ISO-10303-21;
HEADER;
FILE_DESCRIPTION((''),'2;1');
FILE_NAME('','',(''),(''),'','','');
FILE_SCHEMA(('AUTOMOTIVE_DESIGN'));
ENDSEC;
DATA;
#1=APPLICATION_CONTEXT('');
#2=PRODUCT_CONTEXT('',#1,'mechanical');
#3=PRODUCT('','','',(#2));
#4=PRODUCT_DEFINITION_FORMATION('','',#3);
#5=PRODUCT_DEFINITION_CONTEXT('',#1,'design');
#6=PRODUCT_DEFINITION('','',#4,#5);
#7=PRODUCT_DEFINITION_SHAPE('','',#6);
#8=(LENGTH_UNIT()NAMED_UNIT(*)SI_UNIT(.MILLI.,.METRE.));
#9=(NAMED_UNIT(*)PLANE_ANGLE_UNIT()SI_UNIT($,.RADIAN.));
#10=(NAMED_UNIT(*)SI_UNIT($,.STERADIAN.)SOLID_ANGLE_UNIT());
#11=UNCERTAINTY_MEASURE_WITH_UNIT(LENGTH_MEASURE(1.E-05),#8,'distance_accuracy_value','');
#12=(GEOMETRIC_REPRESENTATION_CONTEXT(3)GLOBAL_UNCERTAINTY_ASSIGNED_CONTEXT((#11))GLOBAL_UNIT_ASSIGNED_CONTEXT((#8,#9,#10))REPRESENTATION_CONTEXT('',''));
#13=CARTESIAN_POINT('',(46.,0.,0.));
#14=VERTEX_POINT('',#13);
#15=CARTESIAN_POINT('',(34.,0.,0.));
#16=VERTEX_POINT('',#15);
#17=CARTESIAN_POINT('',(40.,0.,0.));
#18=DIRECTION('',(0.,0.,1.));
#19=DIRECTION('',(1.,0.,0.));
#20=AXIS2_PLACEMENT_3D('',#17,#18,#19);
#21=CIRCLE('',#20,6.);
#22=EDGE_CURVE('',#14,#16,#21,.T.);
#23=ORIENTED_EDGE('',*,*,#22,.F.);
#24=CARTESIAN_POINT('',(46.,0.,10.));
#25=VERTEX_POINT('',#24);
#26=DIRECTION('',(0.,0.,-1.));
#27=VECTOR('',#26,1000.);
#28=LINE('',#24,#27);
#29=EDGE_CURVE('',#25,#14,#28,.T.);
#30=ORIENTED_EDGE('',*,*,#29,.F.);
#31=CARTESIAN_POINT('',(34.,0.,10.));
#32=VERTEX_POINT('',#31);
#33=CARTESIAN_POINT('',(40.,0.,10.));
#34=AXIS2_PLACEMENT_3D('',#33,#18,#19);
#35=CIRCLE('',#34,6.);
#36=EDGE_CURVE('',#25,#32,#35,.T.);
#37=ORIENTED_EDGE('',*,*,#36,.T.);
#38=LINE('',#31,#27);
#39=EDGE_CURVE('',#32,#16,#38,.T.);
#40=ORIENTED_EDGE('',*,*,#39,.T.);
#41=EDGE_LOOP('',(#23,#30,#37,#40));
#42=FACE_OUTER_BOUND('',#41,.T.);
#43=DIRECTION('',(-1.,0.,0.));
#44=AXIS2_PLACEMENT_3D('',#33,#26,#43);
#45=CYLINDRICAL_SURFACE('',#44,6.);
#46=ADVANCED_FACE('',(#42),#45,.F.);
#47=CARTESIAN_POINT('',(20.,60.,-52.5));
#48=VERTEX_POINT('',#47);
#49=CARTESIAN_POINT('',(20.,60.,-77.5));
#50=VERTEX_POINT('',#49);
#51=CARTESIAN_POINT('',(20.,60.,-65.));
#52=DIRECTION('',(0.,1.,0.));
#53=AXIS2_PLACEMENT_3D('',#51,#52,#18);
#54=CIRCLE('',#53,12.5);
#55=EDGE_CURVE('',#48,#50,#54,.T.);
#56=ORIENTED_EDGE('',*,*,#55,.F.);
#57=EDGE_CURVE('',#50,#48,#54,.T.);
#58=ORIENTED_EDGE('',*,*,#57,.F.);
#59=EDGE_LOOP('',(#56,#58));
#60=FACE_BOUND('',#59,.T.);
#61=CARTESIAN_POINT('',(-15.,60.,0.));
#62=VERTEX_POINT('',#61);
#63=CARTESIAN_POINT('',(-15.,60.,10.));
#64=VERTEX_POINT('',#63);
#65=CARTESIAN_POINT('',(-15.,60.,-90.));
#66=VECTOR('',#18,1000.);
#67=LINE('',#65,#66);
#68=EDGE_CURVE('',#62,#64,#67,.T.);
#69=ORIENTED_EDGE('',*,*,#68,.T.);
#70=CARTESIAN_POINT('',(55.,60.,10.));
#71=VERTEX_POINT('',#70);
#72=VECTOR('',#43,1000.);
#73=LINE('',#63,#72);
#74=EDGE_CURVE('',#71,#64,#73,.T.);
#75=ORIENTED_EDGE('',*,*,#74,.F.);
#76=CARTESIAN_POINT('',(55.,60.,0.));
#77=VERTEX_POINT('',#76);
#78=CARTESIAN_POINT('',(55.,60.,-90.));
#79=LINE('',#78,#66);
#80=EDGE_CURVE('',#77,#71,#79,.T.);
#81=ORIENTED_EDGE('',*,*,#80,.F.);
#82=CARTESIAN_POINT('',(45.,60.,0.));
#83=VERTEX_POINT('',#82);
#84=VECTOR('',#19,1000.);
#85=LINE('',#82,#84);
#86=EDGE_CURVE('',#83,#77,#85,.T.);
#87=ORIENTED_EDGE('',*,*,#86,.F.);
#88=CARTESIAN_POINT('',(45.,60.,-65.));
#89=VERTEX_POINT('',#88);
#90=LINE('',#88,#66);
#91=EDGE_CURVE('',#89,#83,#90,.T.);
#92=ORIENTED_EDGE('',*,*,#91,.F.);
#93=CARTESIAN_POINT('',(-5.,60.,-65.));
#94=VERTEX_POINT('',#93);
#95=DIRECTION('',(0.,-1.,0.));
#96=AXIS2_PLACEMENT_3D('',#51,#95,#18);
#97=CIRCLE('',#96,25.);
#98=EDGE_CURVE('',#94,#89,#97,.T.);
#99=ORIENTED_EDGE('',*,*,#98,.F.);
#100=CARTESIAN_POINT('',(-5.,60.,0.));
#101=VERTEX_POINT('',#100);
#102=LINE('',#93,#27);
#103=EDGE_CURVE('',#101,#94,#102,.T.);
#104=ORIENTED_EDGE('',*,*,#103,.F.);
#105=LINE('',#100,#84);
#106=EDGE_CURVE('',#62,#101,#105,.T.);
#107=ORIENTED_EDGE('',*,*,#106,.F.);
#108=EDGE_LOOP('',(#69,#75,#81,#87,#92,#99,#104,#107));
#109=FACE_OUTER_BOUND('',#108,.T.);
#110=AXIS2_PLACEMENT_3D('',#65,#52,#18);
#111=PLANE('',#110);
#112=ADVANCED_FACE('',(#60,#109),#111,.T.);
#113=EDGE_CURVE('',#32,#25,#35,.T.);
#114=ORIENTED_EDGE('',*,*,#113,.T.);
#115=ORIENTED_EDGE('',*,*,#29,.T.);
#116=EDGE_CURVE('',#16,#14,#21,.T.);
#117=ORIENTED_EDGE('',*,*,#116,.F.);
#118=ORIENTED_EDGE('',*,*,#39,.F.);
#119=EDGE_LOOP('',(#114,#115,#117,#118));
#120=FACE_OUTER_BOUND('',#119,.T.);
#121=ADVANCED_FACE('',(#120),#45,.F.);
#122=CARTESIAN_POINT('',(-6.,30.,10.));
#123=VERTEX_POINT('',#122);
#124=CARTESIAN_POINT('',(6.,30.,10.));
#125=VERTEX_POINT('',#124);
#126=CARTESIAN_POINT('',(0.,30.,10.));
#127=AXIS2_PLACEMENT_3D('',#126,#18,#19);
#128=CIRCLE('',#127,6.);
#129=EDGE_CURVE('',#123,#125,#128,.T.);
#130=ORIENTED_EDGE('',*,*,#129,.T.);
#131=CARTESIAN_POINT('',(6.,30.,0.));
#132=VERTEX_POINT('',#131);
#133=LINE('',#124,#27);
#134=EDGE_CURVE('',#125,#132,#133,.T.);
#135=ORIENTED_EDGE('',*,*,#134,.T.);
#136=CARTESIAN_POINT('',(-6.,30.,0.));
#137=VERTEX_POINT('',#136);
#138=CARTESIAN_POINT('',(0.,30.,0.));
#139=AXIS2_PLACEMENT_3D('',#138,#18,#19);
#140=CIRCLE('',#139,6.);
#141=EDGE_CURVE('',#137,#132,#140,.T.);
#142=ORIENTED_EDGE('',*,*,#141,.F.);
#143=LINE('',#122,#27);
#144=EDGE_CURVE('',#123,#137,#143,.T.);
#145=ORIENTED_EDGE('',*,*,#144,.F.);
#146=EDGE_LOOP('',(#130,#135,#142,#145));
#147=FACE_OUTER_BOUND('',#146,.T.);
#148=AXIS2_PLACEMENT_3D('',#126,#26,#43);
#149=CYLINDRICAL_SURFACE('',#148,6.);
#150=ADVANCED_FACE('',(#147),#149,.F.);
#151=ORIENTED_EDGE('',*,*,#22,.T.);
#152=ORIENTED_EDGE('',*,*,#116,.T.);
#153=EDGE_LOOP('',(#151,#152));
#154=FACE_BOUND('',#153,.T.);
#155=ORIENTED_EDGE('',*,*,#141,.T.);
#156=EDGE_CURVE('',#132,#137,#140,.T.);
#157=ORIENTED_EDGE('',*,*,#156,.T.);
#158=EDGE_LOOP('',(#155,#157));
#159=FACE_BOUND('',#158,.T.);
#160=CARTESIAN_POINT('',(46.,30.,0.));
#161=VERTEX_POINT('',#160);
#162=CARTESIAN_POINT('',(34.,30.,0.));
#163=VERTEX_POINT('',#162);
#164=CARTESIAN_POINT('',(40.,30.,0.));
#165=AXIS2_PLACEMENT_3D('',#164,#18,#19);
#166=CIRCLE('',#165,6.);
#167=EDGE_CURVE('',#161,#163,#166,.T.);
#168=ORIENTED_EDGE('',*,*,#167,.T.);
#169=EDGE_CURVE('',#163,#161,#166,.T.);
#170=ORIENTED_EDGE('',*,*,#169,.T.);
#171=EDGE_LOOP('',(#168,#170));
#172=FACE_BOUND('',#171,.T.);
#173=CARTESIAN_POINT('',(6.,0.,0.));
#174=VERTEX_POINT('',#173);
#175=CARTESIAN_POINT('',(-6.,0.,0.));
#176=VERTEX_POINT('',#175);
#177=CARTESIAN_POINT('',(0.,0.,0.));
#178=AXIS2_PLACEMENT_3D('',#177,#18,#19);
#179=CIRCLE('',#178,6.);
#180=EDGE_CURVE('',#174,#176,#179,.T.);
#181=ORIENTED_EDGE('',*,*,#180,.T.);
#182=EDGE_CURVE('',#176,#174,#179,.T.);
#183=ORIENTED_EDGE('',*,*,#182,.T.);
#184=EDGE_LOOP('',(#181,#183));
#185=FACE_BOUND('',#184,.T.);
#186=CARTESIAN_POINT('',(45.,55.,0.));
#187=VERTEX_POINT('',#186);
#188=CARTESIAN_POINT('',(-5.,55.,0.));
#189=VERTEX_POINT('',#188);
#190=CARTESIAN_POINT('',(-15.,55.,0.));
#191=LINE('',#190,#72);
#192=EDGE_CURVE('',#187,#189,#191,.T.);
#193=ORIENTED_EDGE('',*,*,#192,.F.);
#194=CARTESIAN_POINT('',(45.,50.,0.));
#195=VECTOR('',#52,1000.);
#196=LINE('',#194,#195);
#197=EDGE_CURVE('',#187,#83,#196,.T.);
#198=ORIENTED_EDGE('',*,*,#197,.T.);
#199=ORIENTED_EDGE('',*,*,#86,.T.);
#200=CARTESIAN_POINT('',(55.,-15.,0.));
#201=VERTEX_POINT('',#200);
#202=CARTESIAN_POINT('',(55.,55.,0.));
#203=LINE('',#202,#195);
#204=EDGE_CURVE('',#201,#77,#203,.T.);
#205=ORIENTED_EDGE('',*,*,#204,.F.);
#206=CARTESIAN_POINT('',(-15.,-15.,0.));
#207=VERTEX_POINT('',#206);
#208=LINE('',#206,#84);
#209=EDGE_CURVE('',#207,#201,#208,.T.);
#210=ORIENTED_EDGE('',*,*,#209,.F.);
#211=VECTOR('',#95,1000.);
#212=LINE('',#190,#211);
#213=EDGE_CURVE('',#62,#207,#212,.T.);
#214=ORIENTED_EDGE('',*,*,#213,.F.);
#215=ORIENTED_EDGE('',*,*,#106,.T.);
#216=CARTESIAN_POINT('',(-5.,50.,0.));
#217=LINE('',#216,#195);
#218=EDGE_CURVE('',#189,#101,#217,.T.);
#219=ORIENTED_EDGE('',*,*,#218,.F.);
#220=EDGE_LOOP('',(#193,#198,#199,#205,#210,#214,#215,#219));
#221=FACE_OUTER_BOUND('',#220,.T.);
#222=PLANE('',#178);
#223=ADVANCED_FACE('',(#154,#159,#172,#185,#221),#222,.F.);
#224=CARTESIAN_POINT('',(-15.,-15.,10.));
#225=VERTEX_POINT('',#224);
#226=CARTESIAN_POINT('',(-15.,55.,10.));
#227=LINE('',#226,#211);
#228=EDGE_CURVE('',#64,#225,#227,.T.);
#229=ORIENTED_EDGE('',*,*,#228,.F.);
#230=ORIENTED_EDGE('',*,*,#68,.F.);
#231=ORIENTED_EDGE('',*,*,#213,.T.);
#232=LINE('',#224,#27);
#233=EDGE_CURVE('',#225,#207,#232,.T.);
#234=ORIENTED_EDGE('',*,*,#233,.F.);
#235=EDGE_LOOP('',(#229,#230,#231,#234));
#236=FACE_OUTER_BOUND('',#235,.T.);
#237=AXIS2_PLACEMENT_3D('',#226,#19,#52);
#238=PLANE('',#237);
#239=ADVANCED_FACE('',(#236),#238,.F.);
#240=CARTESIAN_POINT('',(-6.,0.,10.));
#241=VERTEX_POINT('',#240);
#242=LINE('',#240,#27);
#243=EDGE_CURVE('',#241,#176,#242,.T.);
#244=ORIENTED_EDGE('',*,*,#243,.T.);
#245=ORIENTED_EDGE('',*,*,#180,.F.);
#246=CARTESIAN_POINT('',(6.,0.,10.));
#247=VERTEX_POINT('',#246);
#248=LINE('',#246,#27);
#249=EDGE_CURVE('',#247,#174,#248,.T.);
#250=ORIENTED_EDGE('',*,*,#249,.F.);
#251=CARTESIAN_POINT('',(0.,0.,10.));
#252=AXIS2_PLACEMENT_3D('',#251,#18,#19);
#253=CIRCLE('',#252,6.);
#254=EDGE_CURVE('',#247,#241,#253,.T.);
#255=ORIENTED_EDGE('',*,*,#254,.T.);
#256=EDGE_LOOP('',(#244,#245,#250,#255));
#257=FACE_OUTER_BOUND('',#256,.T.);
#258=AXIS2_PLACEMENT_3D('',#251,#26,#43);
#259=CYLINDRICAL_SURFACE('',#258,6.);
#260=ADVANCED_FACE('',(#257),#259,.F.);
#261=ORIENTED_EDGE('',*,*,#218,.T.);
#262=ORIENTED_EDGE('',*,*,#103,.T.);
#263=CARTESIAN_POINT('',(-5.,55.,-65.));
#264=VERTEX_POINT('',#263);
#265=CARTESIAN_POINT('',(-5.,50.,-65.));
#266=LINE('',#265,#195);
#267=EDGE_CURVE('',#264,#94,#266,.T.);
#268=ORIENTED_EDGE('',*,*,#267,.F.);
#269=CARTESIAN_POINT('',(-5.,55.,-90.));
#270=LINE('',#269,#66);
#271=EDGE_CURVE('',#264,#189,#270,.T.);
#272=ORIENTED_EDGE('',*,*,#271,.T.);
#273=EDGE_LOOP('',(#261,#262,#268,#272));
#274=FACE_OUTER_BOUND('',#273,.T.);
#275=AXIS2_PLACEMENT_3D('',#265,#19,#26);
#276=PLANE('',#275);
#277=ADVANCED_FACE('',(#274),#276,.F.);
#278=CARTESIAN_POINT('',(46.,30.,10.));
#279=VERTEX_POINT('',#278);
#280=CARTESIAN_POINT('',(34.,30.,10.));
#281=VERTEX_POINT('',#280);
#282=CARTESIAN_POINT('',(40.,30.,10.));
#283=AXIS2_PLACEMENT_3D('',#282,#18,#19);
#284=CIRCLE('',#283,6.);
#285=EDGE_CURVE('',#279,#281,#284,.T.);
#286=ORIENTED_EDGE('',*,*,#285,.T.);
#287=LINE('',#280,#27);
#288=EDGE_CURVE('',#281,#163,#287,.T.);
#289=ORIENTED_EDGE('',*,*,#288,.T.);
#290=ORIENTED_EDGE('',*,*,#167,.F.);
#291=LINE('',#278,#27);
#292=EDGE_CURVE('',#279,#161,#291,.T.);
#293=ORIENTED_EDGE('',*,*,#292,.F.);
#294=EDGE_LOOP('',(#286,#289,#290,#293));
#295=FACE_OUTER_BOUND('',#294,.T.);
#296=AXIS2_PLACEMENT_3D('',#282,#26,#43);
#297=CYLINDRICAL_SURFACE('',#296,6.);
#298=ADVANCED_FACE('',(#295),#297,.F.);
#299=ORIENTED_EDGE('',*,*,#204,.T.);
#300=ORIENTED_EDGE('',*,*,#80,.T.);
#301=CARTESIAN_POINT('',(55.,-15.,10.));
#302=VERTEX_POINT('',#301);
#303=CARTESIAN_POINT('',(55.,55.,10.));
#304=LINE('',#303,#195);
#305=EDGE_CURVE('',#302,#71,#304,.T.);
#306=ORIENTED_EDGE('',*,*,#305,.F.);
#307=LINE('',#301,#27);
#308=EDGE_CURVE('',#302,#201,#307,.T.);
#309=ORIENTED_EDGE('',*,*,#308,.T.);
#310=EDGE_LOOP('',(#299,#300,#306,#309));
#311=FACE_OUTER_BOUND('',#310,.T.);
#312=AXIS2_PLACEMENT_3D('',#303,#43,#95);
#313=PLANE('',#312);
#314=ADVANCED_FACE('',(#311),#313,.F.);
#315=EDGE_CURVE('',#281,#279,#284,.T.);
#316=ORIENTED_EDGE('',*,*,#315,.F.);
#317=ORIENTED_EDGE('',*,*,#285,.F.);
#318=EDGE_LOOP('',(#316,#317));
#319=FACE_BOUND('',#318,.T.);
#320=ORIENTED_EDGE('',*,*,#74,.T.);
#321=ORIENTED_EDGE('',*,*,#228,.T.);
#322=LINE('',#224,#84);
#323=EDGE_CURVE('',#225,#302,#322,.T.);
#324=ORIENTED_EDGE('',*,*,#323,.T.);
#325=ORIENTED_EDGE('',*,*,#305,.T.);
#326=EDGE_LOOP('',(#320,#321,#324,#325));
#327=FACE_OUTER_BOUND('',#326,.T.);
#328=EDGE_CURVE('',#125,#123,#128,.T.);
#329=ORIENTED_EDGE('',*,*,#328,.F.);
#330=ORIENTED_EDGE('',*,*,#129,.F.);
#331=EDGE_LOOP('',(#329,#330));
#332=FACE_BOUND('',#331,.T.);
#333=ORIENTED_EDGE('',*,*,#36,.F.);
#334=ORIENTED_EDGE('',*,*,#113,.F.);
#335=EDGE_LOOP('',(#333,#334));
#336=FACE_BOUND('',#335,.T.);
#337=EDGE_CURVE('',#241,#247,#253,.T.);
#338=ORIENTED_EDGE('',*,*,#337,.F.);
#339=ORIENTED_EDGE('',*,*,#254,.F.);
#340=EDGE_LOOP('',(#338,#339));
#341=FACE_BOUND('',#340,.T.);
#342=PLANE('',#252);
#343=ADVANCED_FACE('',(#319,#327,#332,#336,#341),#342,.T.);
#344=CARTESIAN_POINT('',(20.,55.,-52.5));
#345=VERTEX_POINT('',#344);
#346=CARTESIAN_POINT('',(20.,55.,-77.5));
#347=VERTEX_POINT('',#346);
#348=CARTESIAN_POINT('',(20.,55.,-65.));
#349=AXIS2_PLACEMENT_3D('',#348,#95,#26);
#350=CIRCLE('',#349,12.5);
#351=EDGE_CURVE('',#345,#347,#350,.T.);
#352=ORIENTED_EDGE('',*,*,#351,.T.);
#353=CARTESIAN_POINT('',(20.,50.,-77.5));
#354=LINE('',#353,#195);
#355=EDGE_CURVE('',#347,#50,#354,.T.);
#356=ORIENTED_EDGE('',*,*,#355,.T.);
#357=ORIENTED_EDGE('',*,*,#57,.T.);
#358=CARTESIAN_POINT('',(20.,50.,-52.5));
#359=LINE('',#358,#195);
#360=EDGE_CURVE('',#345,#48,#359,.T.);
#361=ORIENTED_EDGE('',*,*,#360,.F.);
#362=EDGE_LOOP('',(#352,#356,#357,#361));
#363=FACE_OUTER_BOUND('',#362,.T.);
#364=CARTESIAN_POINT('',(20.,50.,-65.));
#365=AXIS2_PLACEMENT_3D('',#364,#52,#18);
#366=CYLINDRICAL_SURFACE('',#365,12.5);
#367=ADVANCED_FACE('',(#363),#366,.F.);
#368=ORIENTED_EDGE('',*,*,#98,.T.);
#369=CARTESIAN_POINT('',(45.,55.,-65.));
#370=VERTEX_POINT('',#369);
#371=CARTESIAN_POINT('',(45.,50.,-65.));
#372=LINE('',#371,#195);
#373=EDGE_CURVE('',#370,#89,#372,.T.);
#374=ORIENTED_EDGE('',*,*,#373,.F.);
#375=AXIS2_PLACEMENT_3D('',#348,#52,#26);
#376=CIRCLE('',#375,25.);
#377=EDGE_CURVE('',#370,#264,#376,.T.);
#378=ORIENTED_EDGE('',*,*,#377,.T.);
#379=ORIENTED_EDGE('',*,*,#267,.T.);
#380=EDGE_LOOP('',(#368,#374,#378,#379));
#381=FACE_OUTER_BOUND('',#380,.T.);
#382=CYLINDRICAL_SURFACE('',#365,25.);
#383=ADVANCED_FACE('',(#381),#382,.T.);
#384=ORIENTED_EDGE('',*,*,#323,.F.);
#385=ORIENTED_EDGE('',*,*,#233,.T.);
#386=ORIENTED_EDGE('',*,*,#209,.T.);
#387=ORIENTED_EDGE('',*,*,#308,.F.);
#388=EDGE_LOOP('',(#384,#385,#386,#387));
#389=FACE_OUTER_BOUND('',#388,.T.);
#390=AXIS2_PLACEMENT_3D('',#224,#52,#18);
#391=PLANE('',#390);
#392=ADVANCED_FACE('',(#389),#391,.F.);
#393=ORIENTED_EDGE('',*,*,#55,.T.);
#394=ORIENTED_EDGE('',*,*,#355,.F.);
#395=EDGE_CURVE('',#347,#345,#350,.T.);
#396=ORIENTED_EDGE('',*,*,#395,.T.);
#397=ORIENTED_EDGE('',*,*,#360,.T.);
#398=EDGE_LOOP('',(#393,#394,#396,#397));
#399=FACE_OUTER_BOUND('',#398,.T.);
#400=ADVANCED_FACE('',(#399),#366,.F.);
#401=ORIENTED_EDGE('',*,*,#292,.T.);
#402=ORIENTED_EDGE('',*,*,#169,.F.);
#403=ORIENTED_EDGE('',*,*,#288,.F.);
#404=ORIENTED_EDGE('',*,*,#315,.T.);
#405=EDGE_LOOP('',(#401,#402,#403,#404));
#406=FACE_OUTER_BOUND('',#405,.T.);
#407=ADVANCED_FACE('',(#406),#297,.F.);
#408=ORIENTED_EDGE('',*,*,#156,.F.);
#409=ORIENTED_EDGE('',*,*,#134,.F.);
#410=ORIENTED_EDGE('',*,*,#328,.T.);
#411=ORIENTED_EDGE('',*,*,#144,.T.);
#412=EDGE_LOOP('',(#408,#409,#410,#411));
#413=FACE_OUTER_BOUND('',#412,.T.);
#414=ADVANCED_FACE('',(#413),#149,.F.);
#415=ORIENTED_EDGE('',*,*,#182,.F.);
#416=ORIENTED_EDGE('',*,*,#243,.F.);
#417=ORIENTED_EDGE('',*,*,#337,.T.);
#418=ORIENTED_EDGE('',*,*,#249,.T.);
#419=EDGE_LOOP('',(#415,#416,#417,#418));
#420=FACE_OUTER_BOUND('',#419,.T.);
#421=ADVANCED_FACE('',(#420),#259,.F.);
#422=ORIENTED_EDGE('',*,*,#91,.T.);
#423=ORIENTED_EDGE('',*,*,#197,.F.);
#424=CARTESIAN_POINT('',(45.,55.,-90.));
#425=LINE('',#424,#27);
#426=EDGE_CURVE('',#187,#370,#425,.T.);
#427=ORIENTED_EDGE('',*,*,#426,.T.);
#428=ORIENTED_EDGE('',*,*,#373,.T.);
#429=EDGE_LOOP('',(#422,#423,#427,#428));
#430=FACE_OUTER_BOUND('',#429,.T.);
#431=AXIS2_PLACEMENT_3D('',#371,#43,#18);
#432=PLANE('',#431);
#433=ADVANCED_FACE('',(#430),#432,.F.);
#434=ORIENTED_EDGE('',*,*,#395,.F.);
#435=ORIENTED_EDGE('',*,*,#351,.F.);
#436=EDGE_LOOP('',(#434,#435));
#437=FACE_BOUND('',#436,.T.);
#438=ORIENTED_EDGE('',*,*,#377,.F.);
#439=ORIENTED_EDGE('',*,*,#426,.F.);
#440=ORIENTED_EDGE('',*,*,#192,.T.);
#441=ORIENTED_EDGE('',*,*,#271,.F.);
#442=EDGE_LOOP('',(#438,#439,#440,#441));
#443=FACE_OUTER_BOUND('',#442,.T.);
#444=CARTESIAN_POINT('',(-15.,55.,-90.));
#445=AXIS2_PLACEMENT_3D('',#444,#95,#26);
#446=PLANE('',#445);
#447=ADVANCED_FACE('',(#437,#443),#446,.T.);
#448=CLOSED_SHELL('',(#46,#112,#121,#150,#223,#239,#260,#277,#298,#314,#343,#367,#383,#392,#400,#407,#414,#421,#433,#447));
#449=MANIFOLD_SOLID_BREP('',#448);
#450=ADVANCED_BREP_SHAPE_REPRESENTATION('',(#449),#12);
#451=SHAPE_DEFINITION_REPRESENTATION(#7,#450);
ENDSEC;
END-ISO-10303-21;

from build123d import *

# Parameters (mm, degrees)
SKETCH_1_W          = 70
SKETCH_1_H          = 70
SKETCH_1_R          = 6
EXTRUDE_1_DEPTH     = 10
SKETCH_2_W          = 70
SKETCH_2_H          = 5
EXTRUDE_2_DEPTH     = 100
SKETCH_4_R          = 12.5
CUT_EXTRUDE_1_DEPTH = 10


with BuildPart() as part:
    # 草图1 → 凸台-拉伸1 (new body)
    with BuildSketch(Plane.XY):
        with Locations((20, 20)):
            Rectangle(SKETCH_1_W, SKETCH_1_H)
        Circle(SKETCH_1_R, mode=Mode.SUBTRACT)
        with Locations((0, 30)):
            Circle(SKETCH_1_R, mode=Mode.SUBTRACT)
        with Locations((40, 30)):
            Circle(SKETCH_1_R, mode=Mode.SUBTRACT)
        with Locations((40, 0)):
            Circle(SKETCH_1_R, mode=Mode.SUBTRACT)
    extrude(amount=EXTRUDE_1_DEPTH)

    # 草图2 → 凸台-拉伸2 (add)
    with BuildSketch(Plane.XY.offset(10)):
        with Locations((20, 57.5)):
            Rectangle(SKETCH_2_W, SKETCH_2_H)
    extrude(amount=-EXTRUDE_2_DEPTH)

    # 草图4 → 切除-拉伸1 (cut)
    with BuildSketch(Plane(origin=(0, 60, 0), x_dir=(1, 0, 0), z_dir=(0, 1, 0))):
        with Locations(Location((20, 65, 0), (0, 0, 270))):
            Circle(SKETCH_4_R)
        with BuildLine():
            Line((-5, 65), (-5, 0))
            Line((-5, 0), (-73.267990544, 0))
            Line((-73.267990544, 0), (-73.267990544, 50))
            Line((-73.267990544, 50), (-73.267990544, 103.705684911))
            Line((-73.267990544, 103.705684911), (78.593427938, 103.705684911))
            Line((78.593427938, 103.705684911), (78.593427938, 0))
            Line((78.593427938, 0), (45, 0))
            Line((45, 0), (45, 65))
            ThreePointArc((45, 65), (20, 90), (-5, 65))
        make_face()
    extrude(amount=-CUT_EXTRUDE_1_DEPTH, mode=Mode.SUBTRACT)


solid = part.part
